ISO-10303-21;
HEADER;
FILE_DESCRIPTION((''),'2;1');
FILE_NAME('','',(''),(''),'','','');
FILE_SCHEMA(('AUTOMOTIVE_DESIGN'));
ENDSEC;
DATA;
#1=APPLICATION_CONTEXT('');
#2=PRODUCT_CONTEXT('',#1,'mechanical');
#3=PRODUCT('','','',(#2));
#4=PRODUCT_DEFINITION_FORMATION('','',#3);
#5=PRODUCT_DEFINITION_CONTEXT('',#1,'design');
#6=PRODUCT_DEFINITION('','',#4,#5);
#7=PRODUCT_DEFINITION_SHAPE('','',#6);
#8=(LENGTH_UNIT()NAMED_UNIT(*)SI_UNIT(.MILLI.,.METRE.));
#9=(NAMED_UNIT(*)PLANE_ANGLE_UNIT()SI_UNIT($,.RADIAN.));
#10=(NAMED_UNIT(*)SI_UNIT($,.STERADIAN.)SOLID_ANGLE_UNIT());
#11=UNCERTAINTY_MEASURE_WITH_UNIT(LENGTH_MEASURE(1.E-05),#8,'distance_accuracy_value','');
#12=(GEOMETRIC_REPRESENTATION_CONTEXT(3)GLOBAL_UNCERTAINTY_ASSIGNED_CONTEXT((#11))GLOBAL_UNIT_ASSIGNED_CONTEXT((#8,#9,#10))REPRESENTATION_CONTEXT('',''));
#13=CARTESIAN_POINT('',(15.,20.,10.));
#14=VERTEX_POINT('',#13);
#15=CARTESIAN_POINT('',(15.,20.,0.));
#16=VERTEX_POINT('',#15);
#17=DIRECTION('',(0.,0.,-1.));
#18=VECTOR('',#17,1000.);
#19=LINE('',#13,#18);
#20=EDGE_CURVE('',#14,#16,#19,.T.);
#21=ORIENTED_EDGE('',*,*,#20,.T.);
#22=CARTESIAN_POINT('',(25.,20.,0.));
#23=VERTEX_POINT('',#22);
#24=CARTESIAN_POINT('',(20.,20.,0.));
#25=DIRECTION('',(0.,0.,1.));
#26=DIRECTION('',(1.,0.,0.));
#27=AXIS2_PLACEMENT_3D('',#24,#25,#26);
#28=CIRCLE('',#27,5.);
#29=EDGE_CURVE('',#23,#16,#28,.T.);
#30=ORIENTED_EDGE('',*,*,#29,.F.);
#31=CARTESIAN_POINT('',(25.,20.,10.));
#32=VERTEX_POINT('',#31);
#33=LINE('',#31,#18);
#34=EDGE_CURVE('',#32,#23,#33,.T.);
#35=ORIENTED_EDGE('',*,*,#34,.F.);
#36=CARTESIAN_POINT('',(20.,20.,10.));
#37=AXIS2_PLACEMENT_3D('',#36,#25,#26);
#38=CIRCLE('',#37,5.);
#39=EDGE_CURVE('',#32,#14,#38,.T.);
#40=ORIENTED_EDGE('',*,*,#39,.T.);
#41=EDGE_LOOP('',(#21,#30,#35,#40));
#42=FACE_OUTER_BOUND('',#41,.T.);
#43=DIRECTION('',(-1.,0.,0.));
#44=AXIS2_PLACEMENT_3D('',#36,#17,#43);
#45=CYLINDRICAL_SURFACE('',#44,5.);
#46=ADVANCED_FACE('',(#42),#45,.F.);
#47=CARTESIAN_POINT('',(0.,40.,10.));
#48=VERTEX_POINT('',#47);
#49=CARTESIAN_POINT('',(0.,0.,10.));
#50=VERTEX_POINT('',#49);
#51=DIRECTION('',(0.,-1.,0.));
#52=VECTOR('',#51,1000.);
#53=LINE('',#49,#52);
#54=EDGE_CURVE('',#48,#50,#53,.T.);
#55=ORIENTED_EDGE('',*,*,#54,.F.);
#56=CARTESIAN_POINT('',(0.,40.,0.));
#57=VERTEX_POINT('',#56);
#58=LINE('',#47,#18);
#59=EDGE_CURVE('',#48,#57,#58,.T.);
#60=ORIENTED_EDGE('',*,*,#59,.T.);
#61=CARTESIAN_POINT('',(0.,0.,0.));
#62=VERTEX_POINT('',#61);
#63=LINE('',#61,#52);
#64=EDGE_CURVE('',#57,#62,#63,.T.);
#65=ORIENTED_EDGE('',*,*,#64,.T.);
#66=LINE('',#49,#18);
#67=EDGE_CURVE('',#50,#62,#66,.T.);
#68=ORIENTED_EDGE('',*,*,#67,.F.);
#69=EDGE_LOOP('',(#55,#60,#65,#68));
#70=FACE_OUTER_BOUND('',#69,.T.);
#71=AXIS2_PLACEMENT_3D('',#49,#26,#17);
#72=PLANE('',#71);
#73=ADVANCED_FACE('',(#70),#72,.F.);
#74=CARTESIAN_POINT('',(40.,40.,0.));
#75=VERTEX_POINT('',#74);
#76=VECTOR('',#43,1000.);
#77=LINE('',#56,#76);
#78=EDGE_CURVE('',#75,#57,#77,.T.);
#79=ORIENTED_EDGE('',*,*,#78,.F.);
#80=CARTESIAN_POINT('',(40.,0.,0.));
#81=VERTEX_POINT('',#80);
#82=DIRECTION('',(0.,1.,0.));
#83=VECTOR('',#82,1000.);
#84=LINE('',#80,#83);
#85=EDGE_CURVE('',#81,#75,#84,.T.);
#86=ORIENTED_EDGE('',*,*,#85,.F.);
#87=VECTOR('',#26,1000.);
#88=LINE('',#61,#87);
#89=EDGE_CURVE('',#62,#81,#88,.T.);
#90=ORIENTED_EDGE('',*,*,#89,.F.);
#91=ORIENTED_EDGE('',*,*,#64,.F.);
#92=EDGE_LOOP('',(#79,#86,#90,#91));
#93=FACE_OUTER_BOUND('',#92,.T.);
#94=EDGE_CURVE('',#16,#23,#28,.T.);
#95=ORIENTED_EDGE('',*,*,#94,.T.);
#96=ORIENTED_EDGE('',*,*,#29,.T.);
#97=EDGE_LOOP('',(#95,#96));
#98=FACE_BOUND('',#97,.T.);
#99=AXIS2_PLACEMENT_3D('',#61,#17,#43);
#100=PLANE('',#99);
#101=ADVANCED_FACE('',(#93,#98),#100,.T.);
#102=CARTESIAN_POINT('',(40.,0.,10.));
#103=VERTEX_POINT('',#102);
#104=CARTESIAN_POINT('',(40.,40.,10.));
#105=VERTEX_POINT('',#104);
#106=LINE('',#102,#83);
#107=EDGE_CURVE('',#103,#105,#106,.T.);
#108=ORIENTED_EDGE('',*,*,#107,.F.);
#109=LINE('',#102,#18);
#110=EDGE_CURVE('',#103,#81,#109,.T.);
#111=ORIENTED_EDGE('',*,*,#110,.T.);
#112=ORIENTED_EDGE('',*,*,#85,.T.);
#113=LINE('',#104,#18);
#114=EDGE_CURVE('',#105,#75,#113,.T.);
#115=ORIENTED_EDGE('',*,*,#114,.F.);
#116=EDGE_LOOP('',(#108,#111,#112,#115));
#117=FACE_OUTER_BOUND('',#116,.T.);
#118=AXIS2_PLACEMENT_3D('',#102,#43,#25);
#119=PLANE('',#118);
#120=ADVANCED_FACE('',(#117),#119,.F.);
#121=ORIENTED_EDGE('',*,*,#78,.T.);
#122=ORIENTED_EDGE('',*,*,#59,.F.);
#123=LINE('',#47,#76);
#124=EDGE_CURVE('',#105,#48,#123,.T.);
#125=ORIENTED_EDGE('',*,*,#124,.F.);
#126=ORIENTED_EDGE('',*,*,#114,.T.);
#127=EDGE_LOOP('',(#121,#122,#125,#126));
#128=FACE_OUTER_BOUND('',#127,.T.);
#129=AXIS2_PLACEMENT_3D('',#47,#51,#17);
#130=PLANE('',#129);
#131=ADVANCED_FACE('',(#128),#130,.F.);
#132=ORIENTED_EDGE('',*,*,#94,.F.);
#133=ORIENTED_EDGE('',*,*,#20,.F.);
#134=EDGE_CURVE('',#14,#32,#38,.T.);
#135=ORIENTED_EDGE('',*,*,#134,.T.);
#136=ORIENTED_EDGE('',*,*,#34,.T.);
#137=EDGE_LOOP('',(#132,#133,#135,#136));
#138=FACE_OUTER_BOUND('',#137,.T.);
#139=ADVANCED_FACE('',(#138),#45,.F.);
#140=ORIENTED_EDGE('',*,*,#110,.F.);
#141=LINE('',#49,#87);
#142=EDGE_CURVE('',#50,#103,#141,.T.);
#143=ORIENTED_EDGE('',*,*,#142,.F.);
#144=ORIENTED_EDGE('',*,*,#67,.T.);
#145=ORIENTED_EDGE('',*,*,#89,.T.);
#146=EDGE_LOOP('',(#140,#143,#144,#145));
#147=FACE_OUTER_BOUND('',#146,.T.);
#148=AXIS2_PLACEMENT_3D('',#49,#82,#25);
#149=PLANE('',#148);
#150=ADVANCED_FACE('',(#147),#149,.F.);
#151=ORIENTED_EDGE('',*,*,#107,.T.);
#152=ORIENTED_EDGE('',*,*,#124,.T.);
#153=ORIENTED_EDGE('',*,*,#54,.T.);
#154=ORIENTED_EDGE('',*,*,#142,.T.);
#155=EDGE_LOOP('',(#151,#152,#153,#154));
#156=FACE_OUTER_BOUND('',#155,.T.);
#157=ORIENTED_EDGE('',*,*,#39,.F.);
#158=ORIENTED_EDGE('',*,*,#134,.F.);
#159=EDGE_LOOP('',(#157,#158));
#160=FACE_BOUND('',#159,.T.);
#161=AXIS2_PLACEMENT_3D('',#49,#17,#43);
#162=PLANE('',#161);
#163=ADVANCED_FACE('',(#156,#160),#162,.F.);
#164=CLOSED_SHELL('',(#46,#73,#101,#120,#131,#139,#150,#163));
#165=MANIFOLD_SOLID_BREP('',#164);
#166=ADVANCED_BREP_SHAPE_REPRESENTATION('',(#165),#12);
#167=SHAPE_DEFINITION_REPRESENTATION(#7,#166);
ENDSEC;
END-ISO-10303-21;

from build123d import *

# Parameters (mm, degrees)
SKETCH1_W           = 40
SKETCH1_H           = 40
SKETCH1_R           = 5
BOSS_EXTRUDE1_DEPTH = 10


with BuildPart() as part:
    # Sketch1 → Boss-Extrude1 (new body)
    with BuildSketch(Plane.XY):
        with Locations((20, 20)):
            Rectangle(SKETCH1_W, SKETCH1_H)
        with Locations((20, 20)):
            Circle(SKETCH1_R, mode=Mode.SUBTRACT)
    extrude(amount=BOSS_EXTRUDE1_DEPTH)


solid = part.part
